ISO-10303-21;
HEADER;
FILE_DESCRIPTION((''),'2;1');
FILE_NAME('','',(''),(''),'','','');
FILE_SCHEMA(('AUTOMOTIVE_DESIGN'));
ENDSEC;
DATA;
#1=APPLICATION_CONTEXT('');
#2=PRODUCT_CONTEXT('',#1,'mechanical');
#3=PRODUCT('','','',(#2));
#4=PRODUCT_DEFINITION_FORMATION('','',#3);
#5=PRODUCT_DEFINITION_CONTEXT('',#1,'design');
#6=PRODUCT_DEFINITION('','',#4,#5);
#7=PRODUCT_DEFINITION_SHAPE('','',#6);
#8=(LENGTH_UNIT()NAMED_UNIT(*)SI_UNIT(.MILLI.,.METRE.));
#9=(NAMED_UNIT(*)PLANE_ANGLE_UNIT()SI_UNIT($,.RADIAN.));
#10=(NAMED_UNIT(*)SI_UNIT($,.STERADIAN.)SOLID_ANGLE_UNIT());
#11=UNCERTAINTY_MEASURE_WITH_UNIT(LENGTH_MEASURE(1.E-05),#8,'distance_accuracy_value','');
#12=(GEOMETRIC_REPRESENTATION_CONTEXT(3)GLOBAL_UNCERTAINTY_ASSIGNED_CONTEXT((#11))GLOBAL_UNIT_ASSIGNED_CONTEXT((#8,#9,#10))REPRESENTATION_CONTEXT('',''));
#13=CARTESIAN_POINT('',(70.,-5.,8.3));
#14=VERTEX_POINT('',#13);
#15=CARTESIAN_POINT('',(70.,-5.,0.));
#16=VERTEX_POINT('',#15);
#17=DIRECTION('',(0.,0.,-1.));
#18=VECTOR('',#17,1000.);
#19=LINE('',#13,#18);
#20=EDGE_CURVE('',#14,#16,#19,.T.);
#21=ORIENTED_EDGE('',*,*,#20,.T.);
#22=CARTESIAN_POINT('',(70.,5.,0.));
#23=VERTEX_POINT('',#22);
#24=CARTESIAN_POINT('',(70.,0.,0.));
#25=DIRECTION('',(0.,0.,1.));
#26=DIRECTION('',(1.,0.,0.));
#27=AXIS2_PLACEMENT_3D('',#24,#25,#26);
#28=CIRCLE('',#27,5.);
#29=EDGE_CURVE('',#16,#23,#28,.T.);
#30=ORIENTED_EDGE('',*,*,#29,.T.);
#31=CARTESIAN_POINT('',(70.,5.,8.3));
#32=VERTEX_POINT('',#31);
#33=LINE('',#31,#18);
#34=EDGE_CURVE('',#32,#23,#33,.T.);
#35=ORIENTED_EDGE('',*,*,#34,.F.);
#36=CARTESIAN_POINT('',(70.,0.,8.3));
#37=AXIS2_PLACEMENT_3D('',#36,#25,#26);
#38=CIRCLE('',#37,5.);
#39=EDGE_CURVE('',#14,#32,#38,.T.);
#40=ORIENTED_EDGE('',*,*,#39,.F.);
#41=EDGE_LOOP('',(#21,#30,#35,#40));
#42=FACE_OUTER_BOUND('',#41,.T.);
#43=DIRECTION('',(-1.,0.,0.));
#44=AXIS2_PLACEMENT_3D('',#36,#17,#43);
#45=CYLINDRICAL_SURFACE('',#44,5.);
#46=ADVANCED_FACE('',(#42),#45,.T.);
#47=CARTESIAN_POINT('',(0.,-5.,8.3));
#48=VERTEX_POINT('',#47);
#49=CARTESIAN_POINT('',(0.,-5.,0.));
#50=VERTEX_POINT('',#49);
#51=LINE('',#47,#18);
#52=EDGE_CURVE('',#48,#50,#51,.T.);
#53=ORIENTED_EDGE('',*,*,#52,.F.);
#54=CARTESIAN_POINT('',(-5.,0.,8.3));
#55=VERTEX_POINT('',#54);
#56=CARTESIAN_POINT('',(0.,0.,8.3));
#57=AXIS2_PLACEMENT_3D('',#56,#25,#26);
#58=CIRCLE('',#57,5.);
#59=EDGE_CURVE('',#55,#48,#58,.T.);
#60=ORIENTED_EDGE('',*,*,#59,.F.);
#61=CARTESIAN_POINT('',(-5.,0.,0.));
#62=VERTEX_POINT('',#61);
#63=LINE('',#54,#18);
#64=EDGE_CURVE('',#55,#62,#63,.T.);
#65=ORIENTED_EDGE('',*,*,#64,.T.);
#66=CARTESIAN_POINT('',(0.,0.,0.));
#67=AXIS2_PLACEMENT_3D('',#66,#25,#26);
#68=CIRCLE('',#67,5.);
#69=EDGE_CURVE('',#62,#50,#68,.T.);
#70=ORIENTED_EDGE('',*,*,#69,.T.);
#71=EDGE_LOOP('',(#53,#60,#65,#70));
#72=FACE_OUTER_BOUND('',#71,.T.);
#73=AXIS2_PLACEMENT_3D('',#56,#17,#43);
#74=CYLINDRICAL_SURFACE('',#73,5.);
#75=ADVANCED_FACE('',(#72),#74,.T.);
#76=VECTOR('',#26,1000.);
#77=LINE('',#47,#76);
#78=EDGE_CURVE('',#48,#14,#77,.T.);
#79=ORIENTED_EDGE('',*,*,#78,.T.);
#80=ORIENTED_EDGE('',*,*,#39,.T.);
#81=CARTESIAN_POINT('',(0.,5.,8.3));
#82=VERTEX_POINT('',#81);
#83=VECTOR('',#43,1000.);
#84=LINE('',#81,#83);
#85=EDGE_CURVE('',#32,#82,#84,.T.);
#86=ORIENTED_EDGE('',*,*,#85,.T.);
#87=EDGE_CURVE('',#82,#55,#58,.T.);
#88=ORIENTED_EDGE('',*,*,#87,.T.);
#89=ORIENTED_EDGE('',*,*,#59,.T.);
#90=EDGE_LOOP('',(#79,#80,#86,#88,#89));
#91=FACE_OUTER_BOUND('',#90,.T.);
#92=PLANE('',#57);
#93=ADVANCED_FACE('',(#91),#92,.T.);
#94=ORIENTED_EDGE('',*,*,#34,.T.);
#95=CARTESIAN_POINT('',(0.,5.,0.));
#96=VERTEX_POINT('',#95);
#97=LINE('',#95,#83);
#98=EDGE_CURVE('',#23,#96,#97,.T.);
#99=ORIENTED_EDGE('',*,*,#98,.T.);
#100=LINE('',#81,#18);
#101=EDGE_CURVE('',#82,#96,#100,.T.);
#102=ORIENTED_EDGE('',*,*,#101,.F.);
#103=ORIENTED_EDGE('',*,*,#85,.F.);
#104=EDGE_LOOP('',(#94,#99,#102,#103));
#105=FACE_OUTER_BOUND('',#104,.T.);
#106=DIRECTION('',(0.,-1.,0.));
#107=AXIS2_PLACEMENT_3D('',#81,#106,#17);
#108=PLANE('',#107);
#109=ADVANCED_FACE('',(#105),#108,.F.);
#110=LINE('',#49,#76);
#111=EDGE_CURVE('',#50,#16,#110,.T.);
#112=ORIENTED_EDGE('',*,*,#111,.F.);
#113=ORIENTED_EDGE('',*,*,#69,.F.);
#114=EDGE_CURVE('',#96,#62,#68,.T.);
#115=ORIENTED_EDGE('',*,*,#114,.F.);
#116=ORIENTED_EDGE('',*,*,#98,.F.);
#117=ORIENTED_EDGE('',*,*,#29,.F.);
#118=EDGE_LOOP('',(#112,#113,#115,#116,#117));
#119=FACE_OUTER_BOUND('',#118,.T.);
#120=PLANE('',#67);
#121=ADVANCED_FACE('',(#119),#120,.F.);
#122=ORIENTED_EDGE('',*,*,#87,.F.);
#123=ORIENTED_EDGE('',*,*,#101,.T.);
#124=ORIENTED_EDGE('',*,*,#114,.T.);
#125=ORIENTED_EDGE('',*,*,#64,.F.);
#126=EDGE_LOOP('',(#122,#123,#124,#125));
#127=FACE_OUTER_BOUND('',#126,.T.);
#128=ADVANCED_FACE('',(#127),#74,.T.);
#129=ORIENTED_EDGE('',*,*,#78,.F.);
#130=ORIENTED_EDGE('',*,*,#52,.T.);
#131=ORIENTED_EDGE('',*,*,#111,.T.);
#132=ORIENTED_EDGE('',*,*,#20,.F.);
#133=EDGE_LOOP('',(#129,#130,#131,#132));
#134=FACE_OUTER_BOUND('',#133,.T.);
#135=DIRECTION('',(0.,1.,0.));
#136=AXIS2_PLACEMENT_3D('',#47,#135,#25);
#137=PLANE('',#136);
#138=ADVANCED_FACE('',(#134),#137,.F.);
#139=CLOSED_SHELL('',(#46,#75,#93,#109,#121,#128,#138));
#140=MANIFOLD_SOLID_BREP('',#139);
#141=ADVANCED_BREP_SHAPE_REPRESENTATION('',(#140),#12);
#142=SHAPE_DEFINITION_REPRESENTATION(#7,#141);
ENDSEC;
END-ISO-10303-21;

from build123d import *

# Parameters (mm, degrees)
EXTRUDE_1_DEPTH = 8.3


with BuildPart() as part:
    # 草图1 → 凸台-拉伸1 (new body)
    with BuildSketch(Plane.XY):
        with BuildLine():
            Line((0, 5), (70, 5))
            ThreePointArc((70, 5), (75, 0), (70, -5))
            Line((70, -5), (0, -5))
            ThreePointArc((0, -5), (-5, 0), (0, 5))
        make_face()
    extrude(amount=EXTRUDE_1_DEPTH)


solid = part.part
